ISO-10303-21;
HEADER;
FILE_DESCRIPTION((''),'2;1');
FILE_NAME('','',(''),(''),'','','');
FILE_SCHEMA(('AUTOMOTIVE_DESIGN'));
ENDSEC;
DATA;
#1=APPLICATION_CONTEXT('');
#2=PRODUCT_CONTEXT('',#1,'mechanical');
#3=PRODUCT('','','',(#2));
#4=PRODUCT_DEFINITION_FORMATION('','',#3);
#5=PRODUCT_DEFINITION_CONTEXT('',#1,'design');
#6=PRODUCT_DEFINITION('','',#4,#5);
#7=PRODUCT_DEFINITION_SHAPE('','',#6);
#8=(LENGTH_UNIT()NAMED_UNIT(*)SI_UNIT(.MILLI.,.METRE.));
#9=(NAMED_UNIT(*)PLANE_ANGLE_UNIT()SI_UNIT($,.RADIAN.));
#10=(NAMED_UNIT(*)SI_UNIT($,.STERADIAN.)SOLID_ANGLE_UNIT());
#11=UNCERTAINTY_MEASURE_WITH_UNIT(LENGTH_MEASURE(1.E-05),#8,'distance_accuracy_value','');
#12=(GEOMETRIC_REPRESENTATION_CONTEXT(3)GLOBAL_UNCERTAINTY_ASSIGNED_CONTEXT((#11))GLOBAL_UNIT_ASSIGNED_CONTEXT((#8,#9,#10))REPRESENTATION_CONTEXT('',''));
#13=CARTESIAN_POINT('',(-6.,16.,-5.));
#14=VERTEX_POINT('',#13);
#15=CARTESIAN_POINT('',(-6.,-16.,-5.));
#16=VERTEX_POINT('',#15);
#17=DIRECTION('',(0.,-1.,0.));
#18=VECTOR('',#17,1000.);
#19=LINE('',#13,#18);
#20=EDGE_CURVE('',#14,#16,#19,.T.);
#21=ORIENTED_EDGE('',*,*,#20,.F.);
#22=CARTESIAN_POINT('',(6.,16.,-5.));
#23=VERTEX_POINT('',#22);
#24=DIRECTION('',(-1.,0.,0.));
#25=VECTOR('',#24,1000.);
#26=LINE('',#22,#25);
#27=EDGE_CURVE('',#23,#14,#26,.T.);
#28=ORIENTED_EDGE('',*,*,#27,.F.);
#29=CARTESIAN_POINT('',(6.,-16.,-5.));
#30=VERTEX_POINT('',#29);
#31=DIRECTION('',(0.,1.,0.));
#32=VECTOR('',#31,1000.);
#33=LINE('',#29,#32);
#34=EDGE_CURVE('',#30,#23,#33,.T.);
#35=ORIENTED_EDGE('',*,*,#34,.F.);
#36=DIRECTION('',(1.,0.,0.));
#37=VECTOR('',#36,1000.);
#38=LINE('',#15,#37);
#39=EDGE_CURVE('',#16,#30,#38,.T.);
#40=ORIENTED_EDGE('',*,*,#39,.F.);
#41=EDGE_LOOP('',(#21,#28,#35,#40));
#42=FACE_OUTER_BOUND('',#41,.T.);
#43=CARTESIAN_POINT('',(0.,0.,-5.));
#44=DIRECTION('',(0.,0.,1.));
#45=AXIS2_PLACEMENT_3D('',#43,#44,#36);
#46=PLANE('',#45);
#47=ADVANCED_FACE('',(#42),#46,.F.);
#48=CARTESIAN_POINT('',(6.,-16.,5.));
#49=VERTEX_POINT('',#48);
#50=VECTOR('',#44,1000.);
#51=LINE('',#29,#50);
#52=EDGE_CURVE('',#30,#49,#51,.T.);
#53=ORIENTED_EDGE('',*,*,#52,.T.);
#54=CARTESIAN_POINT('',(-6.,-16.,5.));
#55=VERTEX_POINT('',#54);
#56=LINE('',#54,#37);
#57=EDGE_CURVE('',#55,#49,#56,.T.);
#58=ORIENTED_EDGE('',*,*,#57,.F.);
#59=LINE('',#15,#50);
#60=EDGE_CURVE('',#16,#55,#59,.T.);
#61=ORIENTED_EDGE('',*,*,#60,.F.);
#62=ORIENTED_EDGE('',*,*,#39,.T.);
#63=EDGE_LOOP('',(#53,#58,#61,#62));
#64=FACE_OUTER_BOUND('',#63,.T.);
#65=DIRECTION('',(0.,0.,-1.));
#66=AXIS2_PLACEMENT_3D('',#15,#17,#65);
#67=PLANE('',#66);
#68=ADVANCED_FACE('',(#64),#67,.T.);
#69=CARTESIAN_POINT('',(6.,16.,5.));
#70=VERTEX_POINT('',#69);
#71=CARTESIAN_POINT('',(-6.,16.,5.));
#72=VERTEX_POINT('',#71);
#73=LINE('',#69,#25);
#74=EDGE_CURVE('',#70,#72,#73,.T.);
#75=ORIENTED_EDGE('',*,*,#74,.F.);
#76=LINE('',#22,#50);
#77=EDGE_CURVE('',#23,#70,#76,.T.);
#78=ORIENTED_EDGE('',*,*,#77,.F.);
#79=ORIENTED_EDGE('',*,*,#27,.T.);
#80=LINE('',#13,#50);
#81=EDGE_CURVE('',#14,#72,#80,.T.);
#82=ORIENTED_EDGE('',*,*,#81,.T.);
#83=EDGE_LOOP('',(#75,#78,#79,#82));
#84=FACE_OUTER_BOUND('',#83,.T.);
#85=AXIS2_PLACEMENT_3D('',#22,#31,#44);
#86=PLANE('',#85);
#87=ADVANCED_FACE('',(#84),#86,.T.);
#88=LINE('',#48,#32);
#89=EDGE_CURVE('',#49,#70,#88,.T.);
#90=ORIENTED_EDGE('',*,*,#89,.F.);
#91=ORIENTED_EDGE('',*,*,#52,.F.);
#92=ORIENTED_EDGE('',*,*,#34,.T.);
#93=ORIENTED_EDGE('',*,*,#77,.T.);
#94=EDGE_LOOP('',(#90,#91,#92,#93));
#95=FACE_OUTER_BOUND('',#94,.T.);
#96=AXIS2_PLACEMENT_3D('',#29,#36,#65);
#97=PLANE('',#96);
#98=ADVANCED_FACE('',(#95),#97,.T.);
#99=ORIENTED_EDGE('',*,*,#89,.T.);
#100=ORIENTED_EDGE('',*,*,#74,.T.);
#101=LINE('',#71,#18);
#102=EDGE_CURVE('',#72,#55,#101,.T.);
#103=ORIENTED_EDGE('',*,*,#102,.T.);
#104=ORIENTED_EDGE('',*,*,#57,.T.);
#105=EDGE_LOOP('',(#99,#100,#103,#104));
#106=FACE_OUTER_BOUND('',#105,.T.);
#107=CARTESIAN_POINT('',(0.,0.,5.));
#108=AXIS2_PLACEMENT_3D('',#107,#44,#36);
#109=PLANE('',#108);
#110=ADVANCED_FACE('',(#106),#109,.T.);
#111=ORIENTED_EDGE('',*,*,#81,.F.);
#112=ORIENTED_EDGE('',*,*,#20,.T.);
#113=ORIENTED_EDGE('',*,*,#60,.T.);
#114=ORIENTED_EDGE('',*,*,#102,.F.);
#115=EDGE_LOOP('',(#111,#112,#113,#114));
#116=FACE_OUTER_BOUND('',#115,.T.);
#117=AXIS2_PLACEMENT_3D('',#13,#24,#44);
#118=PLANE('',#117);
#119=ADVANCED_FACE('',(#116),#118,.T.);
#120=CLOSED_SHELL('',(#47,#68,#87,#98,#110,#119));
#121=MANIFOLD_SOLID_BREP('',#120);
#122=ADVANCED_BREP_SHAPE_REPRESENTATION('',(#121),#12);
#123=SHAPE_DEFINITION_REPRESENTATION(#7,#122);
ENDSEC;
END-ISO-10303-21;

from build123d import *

# Parameters (mm, degrees)
SKETCH_1_W      = 12
SKETCH_1_H      = 32
EXTRUDE_1_DEPTH = 5


with BuildPart() as part:
    # 草图1 → 凸台-拉伸1 (new, symmetric)
    with BuildSketch(Plane.XY):
        Rectangle(SKETCH_1_W, SKETCH_1_H)
    extrude(amount=EXTRUDE_1_DEPTH, both=True)


solid = part.part
